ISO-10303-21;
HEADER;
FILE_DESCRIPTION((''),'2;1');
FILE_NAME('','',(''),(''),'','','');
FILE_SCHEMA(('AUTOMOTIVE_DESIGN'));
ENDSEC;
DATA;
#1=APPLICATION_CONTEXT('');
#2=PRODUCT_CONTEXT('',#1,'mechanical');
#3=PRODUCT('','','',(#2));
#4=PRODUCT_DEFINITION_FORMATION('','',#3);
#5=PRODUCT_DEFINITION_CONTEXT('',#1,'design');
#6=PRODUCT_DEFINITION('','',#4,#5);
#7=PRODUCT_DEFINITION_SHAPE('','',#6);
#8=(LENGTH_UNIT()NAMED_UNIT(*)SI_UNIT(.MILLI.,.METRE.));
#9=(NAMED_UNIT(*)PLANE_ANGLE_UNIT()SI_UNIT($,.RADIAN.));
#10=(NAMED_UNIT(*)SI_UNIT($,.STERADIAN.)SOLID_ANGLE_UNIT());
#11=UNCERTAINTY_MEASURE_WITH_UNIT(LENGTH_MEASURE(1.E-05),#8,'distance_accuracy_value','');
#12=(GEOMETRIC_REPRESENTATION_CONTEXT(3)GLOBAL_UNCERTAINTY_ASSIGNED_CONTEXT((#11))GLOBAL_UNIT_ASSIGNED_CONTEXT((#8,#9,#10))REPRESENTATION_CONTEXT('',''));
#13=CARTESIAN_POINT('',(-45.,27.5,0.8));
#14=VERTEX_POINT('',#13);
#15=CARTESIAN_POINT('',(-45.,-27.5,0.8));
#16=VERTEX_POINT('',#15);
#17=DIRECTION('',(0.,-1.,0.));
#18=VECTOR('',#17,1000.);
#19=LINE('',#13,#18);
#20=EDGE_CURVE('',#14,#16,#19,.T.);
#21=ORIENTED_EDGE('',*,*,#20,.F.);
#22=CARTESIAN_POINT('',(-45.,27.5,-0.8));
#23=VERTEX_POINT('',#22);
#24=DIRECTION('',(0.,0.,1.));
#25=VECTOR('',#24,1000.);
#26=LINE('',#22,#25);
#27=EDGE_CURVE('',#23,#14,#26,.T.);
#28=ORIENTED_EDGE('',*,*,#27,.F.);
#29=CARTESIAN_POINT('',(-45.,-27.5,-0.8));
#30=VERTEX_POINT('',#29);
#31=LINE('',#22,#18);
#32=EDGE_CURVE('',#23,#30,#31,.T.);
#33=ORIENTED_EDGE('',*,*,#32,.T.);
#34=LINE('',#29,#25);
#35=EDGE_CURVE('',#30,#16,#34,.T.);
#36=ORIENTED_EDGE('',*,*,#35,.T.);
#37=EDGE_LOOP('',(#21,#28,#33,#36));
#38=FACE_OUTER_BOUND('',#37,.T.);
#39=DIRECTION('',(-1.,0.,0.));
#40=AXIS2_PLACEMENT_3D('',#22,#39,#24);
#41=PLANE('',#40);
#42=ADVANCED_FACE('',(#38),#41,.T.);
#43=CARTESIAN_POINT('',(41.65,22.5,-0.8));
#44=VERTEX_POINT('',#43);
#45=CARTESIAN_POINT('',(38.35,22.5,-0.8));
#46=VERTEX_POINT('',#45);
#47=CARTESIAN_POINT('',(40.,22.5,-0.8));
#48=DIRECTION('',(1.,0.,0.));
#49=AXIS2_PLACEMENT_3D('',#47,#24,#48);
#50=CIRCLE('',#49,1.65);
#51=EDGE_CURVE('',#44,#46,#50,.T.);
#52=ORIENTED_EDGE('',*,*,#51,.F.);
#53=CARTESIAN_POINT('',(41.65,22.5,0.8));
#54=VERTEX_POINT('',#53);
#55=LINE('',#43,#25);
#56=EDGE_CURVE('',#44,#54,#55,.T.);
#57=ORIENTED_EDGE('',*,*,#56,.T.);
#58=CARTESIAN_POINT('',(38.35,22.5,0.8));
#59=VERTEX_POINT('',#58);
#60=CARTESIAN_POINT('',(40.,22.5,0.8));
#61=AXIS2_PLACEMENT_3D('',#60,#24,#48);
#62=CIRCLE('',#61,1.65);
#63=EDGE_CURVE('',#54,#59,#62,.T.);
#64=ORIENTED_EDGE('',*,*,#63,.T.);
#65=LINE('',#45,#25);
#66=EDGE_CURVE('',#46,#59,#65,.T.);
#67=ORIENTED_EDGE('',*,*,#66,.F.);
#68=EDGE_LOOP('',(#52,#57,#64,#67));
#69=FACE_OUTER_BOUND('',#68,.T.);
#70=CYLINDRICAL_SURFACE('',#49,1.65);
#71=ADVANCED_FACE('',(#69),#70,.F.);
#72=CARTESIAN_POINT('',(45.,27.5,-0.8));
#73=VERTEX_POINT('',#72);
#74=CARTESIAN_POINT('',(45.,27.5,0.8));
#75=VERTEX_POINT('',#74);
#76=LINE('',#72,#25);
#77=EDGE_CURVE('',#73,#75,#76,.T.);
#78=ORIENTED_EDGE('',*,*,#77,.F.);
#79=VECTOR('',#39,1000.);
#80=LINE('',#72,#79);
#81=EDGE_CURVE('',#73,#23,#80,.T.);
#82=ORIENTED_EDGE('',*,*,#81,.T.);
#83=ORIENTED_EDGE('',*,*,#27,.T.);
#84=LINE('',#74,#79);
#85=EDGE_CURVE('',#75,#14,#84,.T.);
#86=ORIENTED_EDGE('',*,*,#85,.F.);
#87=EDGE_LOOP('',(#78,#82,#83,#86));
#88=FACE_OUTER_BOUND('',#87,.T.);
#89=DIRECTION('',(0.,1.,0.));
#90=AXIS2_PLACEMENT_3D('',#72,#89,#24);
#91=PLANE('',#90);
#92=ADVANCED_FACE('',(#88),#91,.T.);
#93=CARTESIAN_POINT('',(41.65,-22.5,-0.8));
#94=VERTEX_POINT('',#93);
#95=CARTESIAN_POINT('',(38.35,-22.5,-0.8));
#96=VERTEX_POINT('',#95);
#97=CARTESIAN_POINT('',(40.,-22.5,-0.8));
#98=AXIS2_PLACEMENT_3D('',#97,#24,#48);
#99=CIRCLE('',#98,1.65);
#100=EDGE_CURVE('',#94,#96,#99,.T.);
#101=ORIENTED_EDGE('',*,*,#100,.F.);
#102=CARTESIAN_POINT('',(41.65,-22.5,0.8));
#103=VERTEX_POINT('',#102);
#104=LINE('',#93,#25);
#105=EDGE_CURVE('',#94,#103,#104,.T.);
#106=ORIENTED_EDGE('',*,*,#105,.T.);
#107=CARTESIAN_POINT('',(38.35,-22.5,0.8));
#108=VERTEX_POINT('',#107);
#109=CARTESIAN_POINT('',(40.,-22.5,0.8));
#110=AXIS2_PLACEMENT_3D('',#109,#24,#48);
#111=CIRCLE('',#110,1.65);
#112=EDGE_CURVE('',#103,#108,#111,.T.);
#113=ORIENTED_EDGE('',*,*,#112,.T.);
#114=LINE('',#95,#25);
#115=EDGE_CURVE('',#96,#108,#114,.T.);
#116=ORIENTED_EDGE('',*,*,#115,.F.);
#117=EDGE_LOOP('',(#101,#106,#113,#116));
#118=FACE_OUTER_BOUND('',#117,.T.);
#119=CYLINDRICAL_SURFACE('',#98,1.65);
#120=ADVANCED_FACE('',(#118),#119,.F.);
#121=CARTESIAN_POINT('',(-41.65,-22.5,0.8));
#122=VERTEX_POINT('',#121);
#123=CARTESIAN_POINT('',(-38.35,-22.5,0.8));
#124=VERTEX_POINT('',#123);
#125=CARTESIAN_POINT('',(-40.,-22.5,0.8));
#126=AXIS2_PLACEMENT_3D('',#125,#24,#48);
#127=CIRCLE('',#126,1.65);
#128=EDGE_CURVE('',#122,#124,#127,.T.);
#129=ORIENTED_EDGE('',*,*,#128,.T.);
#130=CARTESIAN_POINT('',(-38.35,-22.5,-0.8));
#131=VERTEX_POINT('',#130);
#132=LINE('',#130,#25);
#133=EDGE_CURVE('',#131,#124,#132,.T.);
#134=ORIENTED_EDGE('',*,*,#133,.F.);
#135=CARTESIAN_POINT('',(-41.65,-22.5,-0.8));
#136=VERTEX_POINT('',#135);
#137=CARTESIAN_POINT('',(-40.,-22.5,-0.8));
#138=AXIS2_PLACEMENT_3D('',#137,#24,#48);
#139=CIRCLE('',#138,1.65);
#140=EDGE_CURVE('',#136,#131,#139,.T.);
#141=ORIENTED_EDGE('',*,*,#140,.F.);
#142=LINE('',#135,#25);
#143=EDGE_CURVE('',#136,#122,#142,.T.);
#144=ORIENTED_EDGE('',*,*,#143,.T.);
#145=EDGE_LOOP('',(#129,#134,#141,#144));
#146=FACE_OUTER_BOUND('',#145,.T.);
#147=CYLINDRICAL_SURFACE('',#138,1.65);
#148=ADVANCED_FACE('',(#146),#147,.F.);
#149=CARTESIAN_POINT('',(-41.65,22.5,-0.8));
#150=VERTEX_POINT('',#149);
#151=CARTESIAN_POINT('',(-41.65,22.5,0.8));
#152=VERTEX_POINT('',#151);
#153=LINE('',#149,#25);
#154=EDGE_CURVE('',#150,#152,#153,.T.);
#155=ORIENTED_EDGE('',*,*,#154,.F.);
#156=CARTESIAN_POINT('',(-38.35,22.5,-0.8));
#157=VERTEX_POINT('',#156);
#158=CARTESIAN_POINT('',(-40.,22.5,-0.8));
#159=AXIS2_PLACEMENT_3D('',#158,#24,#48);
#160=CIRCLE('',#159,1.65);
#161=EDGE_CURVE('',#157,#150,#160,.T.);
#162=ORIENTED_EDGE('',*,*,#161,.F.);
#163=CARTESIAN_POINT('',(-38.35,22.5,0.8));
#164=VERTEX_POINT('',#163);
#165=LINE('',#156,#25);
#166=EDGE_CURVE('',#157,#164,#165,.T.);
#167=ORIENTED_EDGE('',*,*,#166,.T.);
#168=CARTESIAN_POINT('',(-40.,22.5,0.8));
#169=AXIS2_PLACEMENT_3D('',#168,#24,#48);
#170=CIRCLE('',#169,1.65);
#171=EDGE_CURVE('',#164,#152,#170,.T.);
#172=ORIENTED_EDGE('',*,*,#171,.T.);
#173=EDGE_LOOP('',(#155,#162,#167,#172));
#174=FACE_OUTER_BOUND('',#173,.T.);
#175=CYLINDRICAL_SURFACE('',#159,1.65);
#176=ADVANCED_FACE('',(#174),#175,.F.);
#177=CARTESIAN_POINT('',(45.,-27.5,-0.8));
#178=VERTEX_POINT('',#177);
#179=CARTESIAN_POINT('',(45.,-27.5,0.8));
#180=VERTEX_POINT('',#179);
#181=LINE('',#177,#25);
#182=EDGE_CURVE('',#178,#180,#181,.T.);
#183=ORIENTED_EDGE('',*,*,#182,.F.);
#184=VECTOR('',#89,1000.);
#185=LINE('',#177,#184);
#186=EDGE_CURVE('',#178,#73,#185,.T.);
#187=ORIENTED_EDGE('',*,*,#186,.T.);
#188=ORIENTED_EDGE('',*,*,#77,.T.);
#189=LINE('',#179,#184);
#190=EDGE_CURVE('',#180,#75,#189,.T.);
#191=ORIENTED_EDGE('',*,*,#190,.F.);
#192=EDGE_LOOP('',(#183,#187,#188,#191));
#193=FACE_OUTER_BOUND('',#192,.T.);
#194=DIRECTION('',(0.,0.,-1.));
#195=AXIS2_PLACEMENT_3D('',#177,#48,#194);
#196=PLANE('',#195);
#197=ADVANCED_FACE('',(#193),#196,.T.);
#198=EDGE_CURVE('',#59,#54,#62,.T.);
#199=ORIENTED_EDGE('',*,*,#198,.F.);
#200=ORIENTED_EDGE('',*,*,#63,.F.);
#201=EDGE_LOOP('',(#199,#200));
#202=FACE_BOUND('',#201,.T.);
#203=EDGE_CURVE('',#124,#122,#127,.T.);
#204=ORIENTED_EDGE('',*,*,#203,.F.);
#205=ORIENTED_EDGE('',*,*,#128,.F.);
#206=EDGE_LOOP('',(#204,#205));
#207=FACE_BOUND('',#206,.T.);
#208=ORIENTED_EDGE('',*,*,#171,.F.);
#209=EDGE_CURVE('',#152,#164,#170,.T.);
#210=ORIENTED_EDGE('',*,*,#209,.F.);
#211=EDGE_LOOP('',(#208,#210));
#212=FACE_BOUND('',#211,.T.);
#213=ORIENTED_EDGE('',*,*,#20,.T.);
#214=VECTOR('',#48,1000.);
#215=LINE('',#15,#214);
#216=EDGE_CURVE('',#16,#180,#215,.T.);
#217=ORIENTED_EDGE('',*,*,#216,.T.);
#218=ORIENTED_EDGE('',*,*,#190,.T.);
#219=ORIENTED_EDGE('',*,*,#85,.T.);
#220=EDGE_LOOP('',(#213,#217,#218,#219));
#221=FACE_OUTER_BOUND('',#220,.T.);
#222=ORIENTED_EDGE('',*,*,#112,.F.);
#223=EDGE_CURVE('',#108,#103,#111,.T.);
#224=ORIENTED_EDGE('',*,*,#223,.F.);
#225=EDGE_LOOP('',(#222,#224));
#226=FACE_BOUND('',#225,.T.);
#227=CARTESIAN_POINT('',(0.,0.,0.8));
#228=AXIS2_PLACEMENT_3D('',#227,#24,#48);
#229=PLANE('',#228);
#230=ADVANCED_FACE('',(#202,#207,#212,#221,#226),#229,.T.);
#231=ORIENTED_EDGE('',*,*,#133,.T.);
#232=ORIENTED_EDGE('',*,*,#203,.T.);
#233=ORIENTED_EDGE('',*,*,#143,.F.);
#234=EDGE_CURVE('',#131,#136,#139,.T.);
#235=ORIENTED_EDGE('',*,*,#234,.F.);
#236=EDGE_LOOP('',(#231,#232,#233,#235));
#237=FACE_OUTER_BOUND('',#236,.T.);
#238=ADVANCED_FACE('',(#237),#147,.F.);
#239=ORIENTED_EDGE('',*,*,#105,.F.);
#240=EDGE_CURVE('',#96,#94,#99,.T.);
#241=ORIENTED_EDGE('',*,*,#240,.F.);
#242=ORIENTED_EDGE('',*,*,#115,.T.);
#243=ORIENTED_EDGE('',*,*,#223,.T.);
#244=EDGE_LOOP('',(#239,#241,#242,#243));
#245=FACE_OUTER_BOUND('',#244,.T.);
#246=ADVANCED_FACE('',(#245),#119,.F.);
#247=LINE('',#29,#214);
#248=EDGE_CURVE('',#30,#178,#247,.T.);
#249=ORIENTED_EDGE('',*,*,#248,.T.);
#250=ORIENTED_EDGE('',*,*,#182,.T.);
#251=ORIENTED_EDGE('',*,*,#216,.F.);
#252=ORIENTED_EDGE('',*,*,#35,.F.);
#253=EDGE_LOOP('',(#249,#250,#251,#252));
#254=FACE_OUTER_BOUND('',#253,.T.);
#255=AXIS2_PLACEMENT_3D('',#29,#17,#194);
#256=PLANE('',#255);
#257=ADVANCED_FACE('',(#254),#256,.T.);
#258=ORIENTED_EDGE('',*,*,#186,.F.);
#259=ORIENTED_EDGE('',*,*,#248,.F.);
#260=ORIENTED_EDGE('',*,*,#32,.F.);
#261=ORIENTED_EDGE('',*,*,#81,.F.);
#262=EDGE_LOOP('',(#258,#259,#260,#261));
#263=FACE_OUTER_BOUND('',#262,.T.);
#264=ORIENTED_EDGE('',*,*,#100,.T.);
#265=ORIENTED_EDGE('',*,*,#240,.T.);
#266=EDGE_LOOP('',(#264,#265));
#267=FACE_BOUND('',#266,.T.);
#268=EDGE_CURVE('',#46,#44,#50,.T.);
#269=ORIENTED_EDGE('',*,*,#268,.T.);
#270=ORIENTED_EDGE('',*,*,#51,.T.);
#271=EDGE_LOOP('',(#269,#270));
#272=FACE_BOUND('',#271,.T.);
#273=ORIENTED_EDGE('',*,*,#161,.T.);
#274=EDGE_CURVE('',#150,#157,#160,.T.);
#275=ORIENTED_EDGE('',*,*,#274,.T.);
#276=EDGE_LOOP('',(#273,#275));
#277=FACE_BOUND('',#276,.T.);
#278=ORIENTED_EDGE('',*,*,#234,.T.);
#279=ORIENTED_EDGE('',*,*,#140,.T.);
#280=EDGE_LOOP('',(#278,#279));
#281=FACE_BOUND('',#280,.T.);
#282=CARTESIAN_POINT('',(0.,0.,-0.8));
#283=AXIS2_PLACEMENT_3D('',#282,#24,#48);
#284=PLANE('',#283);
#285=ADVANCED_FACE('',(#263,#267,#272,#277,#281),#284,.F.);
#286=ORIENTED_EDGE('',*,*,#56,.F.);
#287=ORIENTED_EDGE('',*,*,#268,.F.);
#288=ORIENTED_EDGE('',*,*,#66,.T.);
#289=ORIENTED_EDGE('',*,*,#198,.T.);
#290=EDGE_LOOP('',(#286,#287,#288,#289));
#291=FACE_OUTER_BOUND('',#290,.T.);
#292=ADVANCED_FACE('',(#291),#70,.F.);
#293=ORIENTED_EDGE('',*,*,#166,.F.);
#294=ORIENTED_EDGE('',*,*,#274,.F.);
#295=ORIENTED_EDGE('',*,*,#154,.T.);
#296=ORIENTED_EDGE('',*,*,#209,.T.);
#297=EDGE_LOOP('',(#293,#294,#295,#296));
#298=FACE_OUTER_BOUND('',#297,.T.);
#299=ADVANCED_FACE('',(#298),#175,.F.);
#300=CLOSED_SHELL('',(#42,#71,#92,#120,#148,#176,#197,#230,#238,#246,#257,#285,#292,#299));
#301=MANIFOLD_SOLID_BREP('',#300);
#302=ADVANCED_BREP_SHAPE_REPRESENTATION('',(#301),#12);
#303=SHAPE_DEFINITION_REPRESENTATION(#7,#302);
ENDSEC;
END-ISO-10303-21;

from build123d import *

# Parameters (mm, degrees)
SKETCH_1_W      = 90
SKETCH_1_H      = 55
SKETCH_1_R      = 1.65
EXTRUDE_1_DEPTH = 0.8


with BuildPart() as part:
    # 草图1 → 凸台-拉伸1 (new, symmetric)
    with BuildSketch(Plane.XY):
        Rectangle(SKETCH_1_W, SKETCH_1_H)
        with Locations((-40, -22.5)):
            Circle(SKETCH_1_R, mode=Mode.SUBTRACT)
        with Locations((-40, 22.5)):
            Circle(SKETCH_1_R, mode=Mode.SUBTRACT)
        with Locations((40, -22.5)):
            Circle(SKETCH_1_R, mode=Mode.SUBTRACT)
        with Locations((40, 22.5)):
            Circle(SKETCH_1_R, mode=Mode.SUBTRACT)
    extrude(amount=EXTRUDE_1_DEPTH, both=True)


solid = part.part
